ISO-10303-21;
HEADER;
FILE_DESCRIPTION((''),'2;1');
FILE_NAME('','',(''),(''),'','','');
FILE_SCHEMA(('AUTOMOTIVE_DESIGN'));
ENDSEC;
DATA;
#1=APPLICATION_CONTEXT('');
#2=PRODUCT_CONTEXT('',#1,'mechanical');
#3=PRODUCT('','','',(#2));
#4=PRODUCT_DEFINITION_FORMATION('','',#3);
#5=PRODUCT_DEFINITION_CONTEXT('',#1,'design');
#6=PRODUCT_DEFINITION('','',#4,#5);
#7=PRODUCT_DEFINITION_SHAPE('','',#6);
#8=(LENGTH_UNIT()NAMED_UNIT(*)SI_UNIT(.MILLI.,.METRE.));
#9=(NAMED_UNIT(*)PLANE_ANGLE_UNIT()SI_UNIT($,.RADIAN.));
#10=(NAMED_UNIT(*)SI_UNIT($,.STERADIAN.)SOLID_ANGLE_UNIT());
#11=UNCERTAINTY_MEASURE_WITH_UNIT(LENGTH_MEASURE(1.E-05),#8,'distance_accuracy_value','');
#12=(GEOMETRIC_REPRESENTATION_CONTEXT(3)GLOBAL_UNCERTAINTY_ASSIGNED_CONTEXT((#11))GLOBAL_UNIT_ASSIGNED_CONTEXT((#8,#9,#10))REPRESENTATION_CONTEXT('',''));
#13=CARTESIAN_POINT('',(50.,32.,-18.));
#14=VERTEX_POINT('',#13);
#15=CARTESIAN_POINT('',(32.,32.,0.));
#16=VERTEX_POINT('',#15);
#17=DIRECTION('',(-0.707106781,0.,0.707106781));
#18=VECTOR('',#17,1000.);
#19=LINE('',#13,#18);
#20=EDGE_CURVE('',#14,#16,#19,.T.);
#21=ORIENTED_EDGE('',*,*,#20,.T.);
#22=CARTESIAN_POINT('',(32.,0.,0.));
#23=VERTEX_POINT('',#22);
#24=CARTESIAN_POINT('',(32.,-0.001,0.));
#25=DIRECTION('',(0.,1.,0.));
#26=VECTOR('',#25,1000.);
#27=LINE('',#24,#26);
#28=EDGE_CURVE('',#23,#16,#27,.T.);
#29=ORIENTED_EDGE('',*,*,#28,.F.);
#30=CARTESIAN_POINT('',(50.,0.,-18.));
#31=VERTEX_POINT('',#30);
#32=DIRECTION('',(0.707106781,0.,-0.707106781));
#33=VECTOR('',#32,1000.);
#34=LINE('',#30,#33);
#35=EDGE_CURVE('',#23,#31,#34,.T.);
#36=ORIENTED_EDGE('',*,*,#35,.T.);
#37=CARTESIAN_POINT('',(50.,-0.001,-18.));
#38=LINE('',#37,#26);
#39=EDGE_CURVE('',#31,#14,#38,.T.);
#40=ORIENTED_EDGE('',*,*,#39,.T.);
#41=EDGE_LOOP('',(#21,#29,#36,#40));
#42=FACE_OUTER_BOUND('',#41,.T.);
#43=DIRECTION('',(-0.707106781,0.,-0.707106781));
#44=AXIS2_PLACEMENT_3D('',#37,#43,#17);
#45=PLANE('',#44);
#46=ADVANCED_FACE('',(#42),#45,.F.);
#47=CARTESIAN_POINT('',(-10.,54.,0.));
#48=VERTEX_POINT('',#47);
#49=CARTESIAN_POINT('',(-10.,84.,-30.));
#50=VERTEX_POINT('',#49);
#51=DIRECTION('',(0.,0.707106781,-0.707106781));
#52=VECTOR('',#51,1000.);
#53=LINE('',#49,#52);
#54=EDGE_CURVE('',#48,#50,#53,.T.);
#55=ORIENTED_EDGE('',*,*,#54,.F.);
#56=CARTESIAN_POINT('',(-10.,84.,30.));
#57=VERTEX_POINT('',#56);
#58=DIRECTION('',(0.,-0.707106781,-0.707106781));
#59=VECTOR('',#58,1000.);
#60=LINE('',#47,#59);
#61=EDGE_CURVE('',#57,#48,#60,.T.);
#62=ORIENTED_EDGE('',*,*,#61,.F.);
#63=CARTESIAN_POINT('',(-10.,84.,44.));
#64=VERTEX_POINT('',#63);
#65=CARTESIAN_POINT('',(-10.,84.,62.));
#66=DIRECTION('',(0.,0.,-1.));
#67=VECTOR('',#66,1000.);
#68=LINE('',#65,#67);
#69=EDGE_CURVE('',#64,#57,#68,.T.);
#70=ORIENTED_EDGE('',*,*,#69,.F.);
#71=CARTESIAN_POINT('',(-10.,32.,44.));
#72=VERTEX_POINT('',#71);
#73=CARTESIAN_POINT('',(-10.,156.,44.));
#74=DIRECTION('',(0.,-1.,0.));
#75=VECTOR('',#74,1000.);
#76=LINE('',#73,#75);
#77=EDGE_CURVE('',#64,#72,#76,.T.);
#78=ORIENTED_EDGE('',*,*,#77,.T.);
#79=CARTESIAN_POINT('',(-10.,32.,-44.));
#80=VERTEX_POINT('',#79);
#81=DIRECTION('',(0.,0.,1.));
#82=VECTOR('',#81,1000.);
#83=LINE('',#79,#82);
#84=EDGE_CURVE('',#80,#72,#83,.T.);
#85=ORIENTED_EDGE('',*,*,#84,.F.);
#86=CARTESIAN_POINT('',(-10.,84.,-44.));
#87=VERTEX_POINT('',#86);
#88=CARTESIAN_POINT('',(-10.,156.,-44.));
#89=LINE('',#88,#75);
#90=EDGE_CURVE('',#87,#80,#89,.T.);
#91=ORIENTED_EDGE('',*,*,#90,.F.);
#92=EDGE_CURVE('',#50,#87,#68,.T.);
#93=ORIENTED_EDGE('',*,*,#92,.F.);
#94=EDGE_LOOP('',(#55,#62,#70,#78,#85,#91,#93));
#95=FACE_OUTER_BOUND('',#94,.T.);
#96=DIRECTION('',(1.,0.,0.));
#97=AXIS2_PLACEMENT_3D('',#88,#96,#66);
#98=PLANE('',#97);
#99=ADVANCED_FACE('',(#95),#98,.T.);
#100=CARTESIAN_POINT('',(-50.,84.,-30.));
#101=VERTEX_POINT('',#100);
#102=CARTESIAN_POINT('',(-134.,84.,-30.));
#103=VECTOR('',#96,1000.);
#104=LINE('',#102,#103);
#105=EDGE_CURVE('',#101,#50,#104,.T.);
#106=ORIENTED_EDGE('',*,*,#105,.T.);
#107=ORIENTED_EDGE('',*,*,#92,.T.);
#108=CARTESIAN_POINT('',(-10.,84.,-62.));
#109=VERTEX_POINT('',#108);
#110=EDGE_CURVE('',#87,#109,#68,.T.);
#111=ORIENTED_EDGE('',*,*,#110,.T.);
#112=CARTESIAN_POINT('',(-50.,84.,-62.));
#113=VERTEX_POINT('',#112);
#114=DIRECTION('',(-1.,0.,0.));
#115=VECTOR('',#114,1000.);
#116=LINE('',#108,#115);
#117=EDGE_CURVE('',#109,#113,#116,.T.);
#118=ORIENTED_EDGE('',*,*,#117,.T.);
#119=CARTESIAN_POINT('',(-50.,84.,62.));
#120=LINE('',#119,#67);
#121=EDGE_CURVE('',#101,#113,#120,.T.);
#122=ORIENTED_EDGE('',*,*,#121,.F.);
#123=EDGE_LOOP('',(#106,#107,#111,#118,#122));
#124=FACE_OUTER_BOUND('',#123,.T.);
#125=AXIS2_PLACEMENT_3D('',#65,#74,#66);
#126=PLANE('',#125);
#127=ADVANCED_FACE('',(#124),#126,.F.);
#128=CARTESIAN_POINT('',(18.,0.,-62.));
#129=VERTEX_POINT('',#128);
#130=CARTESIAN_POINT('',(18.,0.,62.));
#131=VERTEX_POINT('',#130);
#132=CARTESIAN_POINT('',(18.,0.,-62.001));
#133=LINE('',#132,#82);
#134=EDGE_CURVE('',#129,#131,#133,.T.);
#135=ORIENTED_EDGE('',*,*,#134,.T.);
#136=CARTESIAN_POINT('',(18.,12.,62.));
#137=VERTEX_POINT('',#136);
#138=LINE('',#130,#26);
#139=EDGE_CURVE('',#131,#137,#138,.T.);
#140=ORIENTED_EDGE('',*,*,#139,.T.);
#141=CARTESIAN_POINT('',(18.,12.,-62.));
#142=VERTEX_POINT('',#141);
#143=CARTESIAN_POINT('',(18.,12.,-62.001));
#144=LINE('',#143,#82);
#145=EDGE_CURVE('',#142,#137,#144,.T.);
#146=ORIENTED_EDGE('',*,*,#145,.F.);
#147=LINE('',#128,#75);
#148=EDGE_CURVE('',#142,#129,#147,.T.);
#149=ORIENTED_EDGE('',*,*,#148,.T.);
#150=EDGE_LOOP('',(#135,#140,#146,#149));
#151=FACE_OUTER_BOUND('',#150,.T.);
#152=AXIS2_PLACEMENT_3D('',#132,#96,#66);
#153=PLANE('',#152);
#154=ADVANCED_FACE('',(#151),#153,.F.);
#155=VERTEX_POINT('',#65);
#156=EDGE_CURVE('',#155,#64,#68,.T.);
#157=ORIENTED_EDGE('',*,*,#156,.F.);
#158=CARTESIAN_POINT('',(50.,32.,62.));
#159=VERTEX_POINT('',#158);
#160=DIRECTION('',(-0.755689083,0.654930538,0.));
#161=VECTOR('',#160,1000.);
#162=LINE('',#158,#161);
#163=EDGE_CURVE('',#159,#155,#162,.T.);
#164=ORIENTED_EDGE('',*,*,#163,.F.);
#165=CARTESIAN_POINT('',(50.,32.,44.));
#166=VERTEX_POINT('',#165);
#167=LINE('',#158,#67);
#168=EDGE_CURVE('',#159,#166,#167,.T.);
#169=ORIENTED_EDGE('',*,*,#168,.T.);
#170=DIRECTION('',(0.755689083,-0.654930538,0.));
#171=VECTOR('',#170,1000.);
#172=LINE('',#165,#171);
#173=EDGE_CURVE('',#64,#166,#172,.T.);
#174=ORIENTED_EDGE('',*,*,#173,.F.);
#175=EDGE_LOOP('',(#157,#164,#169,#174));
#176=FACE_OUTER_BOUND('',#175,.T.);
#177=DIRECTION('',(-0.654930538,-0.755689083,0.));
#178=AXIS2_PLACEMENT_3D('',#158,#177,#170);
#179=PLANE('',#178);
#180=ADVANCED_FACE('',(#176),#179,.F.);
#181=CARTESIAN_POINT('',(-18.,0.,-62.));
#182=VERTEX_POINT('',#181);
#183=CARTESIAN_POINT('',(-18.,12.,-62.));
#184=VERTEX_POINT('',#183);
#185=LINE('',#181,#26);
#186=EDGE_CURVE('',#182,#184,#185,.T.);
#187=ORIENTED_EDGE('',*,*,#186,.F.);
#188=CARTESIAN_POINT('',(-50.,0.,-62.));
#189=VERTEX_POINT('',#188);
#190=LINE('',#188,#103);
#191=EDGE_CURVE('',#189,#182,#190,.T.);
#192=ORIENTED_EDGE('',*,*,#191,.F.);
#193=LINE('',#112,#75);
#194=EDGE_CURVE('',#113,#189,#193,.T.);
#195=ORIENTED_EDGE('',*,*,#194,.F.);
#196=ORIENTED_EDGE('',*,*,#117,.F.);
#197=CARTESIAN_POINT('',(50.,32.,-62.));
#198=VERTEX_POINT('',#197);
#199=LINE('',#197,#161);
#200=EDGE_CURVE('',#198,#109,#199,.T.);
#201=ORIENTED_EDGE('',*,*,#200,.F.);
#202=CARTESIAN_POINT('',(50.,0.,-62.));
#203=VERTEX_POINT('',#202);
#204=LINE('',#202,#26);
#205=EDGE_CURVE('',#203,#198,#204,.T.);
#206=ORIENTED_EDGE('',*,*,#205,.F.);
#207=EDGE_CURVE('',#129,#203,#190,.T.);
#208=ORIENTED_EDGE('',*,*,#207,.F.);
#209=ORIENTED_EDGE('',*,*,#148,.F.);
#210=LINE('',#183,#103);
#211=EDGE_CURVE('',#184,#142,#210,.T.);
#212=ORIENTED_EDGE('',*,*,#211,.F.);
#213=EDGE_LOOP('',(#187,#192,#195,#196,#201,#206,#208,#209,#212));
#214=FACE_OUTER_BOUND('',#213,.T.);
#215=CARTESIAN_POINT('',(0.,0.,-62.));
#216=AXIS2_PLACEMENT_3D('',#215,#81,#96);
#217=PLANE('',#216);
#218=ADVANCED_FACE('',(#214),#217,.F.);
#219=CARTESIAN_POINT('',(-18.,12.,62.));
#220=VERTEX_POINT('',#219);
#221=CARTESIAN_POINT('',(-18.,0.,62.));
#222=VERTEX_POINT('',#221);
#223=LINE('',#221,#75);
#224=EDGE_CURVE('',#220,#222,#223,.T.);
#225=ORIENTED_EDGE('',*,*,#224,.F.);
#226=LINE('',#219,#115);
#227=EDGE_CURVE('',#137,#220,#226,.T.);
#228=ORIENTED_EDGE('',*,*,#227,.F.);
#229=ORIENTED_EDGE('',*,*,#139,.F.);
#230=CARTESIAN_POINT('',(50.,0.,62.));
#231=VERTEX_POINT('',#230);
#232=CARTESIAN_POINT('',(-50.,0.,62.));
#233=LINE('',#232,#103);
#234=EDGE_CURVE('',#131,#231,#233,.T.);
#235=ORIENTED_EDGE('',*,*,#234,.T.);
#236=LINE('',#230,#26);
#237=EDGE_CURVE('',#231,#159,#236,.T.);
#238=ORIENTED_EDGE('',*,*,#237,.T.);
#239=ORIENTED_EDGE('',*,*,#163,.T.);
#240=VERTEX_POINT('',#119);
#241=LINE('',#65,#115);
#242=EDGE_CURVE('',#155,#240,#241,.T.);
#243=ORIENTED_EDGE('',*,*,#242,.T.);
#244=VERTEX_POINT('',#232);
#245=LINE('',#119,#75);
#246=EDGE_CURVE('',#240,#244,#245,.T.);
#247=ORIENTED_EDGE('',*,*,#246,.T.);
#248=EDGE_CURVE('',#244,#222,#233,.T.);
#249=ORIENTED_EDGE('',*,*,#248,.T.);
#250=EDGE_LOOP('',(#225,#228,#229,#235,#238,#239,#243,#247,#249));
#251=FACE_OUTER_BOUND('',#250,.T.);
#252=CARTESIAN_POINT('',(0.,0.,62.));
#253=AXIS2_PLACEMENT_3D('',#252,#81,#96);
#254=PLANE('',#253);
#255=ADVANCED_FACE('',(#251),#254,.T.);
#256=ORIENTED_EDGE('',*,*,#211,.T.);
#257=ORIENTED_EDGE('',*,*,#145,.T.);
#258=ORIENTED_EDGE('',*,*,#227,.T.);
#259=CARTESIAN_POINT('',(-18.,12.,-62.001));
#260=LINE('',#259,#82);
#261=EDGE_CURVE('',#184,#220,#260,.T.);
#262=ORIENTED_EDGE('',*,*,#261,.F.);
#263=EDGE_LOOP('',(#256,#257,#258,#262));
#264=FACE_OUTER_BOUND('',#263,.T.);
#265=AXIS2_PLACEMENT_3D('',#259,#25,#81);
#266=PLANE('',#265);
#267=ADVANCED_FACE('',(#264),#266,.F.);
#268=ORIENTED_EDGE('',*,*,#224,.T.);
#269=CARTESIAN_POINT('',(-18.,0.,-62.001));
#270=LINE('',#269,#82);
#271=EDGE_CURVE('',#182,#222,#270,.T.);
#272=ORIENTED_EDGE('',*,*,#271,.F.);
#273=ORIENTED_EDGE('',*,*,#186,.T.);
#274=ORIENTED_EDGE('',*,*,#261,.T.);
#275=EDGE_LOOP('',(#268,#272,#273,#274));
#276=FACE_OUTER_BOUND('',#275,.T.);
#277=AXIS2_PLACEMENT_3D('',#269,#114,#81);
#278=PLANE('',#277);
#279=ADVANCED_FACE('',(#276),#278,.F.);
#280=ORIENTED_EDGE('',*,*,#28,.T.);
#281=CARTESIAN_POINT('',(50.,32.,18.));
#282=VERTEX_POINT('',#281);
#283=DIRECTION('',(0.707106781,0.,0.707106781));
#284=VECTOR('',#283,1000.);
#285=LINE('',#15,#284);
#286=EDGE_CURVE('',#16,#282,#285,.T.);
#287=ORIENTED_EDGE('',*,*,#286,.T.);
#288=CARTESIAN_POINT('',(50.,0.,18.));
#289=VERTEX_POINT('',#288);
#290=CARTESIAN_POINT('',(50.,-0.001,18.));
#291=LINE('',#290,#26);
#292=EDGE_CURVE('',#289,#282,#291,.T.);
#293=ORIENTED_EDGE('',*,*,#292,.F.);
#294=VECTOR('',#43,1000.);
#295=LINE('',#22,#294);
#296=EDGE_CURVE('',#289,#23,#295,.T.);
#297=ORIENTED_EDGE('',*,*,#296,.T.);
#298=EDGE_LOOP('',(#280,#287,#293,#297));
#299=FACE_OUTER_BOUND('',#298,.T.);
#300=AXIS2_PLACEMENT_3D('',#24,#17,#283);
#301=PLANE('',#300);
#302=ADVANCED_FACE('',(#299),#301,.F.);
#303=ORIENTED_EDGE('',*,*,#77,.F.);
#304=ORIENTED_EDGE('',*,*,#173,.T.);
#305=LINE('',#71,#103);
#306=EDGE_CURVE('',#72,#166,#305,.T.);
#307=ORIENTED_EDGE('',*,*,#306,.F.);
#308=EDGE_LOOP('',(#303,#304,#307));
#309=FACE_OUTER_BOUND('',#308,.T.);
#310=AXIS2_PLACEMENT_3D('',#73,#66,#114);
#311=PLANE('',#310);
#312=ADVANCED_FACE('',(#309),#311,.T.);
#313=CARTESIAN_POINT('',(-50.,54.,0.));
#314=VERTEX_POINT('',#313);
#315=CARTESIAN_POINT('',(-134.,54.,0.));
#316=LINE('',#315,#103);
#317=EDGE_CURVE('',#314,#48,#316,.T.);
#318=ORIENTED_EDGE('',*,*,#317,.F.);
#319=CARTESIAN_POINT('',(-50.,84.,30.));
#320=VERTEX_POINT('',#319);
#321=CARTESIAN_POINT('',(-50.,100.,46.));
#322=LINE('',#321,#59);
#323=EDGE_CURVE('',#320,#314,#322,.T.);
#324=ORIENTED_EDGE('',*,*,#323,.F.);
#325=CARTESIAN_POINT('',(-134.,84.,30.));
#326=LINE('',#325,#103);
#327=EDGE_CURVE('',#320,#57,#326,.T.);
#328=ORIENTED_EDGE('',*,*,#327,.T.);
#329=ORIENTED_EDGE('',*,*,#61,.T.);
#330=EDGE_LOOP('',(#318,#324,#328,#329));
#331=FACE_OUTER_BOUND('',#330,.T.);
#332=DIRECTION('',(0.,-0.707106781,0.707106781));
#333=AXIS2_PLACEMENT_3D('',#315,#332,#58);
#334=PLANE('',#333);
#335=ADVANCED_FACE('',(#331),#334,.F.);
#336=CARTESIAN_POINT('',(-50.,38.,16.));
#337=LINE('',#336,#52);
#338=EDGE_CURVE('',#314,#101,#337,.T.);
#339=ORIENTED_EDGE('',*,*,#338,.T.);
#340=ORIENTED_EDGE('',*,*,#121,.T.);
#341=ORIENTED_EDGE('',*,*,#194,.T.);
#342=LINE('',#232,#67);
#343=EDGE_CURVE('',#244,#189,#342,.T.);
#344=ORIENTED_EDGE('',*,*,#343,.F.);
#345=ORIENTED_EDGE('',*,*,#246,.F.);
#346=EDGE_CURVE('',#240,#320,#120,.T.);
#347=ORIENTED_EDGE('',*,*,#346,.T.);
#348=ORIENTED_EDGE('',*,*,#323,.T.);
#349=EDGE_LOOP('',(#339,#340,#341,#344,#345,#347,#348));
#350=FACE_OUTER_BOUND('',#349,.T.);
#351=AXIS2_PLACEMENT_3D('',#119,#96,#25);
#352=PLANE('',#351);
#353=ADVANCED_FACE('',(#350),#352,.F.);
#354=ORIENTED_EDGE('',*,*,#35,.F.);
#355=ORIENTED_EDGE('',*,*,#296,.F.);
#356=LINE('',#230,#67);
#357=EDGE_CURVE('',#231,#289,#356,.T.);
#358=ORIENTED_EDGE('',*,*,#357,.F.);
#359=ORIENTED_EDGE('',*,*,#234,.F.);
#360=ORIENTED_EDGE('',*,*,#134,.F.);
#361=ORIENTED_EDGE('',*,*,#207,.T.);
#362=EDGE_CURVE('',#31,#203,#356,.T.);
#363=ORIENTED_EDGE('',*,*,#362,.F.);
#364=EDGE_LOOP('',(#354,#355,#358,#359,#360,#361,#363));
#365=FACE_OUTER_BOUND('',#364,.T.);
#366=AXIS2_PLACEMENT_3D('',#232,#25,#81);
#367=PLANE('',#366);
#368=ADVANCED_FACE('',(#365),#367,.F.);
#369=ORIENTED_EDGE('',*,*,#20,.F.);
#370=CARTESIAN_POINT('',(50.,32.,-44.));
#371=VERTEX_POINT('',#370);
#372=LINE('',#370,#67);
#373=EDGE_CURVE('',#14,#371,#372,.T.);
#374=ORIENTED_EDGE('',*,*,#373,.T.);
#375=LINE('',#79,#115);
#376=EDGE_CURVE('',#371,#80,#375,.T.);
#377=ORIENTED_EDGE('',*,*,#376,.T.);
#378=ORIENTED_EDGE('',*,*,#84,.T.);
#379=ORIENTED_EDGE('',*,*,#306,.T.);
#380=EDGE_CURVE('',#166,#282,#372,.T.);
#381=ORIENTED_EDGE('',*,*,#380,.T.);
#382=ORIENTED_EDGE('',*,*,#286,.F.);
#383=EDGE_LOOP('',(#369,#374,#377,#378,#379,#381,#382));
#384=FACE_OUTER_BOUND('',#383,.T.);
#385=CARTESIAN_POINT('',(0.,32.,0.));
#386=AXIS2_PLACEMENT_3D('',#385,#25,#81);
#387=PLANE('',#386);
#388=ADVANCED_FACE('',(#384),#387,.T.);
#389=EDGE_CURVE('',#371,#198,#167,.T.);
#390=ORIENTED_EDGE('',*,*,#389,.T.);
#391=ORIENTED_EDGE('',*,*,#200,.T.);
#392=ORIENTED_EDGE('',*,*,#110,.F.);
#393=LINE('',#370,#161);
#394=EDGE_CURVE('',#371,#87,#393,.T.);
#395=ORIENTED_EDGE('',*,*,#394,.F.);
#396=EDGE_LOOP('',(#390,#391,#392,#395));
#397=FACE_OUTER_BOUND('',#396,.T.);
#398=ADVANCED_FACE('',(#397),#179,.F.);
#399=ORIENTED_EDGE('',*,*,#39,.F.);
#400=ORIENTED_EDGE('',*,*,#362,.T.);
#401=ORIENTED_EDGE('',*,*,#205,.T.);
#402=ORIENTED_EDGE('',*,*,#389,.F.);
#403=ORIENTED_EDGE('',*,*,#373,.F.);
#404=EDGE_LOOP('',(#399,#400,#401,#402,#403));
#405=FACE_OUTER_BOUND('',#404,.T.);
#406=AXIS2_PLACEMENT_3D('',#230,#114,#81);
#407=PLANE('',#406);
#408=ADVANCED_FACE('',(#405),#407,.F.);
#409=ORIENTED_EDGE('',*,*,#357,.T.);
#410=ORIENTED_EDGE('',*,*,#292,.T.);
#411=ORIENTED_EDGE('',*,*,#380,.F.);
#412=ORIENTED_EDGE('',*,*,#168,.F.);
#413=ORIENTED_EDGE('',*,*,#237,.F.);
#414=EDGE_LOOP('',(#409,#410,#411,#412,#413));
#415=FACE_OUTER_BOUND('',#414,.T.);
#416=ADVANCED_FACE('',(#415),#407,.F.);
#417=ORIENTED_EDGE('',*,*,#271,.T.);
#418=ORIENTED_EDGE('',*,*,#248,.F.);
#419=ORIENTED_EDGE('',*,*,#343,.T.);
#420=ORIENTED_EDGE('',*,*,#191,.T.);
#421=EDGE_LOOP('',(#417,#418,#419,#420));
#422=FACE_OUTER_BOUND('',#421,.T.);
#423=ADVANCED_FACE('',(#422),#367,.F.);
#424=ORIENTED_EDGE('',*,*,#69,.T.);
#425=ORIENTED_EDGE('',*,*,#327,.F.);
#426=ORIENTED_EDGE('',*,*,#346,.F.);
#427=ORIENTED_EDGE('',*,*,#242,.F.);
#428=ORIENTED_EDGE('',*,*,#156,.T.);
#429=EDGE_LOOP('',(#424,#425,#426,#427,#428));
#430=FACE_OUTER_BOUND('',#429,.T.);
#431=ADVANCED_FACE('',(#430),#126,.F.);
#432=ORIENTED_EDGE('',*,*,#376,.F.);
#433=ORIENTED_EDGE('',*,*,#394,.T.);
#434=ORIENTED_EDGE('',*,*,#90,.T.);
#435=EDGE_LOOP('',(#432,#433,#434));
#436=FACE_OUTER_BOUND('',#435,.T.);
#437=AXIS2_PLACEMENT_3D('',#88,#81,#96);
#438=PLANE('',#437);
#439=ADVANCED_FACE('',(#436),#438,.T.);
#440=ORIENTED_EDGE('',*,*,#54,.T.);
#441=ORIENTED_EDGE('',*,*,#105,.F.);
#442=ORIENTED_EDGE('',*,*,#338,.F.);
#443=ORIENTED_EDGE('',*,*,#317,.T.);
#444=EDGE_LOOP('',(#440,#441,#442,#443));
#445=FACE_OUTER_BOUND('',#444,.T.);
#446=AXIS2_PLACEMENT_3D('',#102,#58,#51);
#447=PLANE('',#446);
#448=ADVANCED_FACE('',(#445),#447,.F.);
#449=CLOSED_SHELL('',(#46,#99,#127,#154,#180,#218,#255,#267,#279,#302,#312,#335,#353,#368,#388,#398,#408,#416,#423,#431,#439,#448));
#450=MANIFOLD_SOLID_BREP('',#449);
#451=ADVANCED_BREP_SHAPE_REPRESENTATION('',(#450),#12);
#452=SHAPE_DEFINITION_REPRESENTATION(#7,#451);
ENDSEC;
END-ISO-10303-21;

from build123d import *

# Parameters (mm, degrees)
SUPPORT_BLOCK_BODY_DEPTH    = 62
CENTRE_START                = 32
CENTRE_CHANNEL_SKETCH_W     = 60
CENTRE_CHANNEL_SKETCH_H     = 88
CENTRE_CHANNEL_CUT_DEPTH    = 124
V_NOTCH_CUT_DEPTH           = 124
BASE_GROOVE_CUT_18X36_REACH = 97.121
FRONT_NOTCH_CUT_REACH       = 159.899
FRONT_NOTCH_SKETCH_W        = 36
FRONT_NOTCH_SKETCH_H        = 12


with BuildPart() as part:
    # Block Profile Sketch → Support Block Body (new, symmetric)
    with BuildSketch(Plane.XY):
        Polygon((-50, 0), (50, 0), (50, 32), (-10, 84), (-50, 84), align=None)
    extrude(amount=SUPPORT_BLOCK_BODY_DEPTH, both=True)

    # Centre Channel Sketch → Centre Channel Cut (cut)
    with BuildSketch(Plane(origin=(0, 0, 0), x_dir=(1, 0, 0), z_dir=(0, 1, 0)).offset(CENTRE_START)):
        with Locations((20, 0)):
            Rectangle(CENTRE_CHANNEL_SKETCH_W, CENTRE_CHANNEL_SKETCH_H)
    extrude(amount=CENTRE_CHANNEL_CUT_DEPTH, mode=Mode.SUBTRACT)

    # V-Notch Sketch → V-Notch Cut (cut)
    with BuildSketch(Plane(origin=(-10, 0, 0), x_dir=(0, 0, -1), z_dir=(1, 0, 0))):
        Polygon((30, 84), (0, 54), (-30, 84), align=None)
    extrude(amount=-V_NOTCH_CUT_DEPTH, mode=Mode.SUBTRACT)

    # Base Groove Sketch → Base Groove Cut 18x36 (cut, up to next)
    with BuildSketch(Plane(origin=(0, 32, 0), x_dir=(1, 0, 0), z_dir=(0, 1, 0)), mode=Mode.PRIVATE) as base_groove_cut_18x36_sk1:
        Polygon((50, 18), (32, 0), (50, -18), align=None)
    base_groove_cut_18x36_tool1 = extrude(base_groove_cut_18x36_sk1.sketch, amount=-BASE_GROOVE_CUT_18X36_REACH, mode=Mode.PRIVATE) & part.part
    add(base_groove_cut_18x36_tool1.solids().sort_by_distance((44, 32, 0))[0], mode=Mode.SUBTRACT)

    # Front Notch Sketch → Front Notch Cut (cut, up to next)
    with BuildSketch(Plane.XY.offset(62), mode=Mode.PRIVATE) as front_notch_cut_sk1:
        with Locations((0, 6)):
            Rectangle(FRONT_NOTCH_SKETCH_W, FRONT_NOTCH_SKETCH_H)
    front_notch_cut_tool1 = extrude(front_notch_cut_sk1.sketch, amount=-FRONT_NOTCH_CUT_REACH, mode=Mode.PRIVATE) & part.part
    add(front_notch_cut_tool1.solids().sort_by_distance((0, 6, 62))[0], mode=Mode.SUBTRACT)


solid = part.part
